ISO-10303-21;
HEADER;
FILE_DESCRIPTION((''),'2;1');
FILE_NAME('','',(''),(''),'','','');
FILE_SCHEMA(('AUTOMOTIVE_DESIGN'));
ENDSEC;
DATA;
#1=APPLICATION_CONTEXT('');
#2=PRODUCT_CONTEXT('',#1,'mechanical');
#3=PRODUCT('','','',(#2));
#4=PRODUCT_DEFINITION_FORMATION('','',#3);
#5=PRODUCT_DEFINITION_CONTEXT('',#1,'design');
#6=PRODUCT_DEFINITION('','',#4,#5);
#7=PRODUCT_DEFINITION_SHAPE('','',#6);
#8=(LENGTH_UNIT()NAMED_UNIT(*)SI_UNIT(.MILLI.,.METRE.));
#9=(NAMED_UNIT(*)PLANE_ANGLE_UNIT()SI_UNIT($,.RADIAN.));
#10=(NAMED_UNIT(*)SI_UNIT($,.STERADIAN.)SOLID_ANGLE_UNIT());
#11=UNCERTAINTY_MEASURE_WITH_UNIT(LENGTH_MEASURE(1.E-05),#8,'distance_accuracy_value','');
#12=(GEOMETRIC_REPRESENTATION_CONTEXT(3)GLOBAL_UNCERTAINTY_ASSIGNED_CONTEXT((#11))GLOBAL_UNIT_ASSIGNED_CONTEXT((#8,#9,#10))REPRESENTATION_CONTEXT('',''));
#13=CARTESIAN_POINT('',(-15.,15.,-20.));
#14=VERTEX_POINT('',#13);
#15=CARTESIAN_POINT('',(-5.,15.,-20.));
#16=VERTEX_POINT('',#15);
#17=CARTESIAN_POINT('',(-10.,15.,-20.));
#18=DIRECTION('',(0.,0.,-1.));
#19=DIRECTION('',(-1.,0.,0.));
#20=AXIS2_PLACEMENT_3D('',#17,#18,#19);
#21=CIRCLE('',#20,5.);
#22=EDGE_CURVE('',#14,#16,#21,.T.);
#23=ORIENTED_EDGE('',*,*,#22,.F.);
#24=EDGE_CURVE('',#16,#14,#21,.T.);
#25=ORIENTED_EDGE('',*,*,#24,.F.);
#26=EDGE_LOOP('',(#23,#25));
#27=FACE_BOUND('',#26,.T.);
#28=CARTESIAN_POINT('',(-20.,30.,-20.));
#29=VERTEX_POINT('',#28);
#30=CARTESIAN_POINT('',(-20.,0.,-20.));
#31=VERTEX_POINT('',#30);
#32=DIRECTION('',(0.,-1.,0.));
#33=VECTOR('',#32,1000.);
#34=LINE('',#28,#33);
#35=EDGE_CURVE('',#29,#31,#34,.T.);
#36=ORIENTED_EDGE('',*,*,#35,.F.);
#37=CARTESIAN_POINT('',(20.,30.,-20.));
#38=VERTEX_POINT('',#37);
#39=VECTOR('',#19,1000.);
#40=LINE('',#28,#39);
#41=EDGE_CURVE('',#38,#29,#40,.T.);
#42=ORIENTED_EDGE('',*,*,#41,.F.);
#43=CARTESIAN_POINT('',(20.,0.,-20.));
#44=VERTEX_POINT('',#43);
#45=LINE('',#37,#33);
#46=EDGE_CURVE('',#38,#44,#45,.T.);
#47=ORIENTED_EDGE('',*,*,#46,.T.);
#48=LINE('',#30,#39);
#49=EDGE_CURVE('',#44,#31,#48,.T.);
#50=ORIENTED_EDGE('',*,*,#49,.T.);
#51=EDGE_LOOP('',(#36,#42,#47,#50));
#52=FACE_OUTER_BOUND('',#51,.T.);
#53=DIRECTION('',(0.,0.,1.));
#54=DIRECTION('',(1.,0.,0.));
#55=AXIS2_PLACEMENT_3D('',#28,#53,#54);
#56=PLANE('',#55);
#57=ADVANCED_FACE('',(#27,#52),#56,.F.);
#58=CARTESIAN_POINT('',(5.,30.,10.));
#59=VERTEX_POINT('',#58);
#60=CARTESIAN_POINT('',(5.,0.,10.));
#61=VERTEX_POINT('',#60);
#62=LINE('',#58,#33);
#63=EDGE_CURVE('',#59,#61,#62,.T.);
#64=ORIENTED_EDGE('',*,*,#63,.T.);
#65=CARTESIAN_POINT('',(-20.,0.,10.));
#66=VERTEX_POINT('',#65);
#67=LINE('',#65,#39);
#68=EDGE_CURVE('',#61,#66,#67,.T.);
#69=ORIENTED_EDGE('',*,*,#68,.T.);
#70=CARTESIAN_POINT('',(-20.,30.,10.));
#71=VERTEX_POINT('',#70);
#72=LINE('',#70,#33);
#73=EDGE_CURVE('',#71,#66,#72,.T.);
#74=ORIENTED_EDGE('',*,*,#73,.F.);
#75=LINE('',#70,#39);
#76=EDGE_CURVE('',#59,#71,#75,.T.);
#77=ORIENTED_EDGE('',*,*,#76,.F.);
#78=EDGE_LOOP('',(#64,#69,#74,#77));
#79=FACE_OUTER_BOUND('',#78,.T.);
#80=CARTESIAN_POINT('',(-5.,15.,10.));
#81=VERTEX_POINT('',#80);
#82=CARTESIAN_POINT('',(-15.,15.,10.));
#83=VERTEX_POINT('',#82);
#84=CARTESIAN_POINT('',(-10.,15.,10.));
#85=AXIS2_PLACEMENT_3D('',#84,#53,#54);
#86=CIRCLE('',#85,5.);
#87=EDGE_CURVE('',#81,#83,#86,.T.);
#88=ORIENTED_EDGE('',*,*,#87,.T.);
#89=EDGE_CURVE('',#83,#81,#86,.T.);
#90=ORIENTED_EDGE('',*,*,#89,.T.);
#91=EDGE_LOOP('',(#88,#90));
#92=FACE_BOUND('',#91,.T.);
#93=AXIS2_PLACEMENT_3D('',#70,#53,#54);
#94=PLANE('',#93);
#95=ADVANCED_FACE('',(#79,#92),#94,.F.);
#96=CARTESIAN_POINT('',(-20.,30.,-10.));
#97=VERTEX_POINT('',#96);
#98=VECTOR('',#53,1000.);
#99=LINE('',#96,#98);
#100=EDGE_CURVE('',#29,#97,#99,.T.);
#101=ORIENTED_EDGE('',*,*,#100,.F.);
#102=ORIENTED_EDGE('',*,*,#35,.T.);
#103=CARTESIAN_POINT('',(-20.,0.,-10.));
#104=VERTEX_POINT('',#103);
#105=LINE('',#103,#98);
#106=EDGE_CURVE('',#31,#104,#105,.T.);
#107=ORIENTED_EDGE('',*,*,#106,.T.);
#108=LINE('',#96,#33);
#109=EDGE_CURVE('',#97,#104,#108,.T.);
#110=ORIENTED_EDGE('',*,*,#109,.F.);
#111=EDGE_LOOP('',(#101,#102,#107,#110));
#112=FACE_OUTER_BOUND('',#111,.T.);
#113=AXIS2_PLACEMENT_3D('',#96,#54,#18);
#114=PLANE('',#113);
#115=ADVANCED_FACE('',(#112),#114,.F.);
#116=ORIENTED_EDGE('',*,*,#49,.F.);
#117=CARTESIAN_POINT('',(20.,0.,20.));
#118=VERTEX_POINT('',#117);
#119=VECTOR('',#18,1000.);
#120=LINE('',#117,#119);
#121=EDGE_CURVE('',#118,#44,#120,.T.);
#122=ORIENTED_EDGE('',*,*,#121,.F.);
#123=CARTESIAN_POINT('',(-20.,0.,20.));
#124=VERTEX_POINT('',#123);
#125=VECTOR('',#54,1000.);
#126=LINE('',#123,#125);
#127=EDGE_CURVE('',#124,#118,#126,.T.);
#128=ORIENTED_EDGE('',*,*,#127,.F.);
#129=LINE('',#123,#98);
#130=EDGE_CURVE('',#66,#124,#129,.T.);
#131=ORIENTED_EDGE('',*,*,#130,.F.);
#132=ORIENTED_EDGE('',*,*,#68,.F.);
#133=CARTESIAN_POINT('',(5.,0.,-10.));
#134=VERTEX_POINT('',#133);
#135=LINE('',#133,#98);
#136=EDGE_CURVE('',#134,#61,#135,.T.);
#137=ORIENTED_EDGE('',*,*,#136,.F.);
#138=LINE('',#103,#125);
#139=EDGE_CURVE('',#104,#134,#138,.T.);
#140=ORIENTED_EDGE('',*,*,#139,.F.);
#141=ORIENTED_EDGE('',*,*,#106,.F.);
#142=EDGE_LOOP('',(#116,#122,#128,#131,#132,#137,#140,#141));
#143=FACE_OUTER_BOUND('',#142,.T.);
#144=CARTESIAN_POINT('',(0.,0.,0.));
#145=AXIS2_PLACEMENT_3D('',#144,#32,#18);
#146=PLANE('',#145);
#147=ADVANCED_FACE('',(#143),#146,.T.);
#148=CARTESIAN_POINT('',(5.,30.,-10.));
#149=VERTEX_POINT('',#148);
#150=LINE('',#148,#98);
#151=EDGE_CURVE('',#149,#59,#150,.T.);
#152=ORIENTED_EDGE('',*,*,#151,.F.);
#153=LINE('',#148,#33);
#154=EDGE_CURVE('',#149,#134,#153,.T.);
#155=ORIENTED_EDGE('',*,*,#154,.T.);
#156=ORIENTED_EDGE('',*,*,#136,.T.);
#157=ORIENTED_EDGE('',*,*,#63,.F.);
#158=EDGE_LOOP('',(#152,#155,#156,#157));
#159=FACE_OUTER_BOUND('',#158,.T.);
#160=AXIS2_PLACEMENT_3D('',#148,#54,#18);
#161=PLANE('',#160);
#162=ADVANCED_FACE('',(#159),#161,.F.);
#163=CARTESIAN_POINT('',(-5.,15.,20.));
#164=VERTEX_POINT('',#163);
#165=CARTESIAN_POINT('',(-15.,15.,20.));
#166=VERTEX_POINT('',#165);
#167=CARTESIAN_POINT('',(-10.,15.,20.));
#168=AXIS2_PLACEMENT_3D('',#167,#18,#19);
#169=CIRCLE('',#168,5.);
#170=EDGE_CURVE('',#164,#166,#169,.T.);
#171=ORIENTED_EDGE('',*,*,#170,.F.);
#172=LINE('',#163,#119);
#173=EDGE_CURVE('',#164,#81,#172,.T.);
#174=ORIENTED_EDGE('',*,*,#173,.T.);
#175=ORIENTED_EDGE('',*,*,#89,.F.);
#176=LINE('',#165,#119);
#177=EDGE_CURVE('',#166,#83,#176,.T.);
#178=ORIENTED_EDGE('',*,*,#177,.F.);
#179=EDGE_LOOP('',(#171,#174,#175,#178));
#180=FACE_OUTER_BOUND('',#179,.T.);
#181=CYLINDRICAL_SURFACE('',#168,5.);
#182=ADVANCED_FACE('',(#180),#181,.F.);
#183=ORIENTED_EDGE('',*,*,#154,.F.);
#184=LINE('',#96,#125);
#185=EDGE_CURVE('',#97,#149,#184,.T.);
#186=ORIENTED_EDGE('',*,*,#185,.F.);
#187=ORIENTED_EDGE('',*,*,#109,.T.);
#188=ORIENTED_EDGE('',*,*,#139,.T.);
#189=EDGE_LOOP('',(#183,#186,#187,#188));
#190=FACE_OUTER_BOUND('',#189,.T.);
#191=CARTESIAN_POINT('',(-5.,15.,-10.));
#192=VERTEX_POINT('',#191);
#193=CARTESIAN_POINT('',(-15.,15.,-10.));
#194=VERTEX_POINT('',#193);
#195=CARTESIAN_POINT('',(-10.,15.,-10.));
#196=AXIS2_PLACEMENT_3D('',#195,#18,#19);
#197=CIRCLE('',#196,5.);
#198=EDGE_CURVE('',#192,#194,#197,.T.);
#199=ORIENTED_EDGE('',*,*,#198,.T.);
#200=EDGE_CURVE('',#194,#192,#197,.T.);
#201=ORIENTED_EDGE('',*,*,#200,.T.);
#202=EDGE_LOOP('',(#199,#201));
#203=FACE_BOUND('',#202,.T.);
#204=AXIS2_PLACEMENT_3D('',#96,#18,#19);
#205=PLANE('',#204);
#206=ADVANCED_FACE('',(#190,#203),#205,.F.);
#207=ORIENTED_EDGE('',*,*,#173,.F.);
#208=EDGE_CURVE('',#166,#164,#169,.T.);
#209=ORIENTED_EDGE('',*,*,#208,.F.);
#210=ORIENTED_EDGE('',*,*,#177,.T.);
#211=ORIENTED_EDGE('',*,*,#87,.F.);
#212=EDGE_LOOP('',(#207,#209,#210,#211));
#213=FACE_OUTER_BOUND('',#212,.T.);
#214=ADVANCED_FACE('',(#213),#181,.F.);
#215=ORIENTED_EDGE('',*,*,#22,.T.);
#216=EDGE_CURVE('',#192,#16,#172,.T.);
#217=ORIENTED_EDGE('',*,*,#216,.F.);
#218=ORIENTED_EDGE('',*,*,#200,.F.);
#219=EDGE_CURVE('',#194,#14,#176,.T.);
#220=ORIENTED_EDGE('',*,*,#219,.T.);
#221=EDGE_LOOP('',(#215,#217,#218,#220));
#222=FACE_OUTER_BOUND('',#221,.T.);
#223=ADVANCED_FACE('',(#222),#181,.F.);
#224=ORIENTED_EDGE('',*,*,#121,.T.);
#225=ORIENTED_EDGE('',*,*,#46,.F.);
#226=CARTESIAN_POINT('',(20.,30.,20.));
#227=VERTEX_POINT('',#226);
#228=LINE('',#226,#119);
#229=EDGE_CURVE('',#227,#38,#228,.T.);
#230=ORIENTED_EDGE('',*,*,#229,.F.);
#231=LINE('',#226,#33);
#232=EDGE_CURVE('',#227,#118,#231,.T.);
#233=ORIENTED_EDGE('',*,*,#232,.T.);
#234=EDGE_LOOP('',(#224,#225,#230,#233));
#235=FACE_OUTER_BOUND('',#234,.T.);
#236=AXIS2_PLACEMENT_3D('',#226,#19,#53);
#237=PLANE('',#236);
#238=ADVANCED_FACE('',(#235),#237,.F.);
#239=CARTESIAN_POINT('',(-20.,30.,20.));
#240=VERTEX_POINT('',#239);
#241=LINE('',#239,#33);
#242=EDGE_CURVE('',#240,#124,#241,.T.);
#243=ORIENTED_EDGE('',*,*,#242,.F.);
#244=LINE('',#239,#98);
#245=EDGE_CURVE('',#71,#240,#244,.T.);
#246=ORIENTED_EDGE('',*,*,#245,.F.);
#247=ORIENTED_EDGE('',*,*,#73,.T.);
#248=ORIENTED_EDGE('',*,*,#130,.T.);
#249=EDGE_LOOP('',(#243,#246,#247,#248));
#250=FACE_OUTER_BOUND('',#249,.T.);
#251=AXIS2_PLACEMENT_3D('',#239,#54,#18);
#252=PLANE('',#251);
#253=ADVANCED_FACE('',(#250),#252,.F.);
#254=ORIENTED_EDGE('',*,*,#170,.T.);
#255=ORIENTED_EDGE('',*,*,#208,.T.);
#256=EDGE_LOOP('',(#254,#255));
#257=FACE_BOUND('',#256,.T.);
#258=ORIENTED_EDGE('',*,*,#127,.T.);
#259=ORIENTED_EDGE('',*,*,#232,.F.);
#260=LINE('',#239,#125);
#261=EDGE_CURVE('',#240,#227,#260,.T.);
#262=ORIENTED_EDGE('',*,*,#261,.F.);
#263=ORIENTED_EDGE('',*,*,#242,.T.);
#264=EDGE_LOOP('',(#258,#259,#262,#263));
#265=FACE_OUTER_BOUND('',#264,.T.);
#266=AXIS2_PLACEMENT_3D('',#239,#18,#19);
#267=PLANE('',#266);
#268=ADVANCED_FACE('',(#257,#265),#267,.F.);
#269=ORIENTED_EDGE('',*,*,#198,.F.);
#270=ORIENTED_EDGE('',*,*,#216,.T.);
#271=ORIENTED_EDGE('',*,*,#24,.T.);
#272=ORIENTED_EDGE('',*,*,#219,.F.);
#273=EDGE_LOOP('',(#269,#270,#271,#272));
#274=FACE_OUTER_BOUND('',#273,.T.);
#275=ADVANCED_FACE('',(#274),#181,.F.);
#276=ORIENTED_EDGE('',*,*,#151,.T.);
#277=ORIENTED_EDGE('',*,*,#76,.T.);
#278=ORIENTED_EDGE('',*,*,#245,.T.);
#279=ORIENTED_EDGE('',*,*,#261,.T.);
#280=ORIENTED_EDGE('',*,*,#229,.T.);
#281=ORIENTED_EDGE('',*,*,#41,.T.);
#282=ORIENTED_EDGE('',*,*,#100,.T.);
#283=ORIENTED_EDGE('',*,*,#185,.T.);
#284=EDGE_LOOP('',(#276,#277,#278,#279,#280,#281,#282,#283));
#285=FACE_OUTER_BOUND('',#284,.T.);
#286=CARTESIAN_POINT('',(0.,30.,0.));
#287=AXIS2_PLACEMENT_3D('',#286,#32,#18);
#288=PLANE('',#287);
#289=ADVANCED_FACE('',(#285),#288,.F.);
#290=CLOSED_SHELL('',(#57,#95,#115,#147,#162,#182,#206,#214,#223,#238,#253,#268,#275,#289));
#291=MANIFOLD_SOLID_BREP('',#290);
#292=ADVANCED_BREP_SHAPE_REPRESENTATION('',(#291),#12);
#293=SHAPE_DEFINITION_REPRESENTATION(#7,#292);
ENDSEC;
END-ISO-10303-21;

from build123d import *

# Parameters (mm, degrees)
BOSS_EXTRUDE1_DEPTH = 30
SKETCH2_R           = 5
CUT_EXTRUDE1_DEPTH  = 54.851648071


with BuildPart() as part:
    # Sketch1 → Boss-Extrude1 (new body)
    with BuildSketch(Plane(origin=(0, 0, 0), x_dir=(1, 0, 0), z_dir=(0, 1, 0))):
        Polygon((-20, 10), (-20, 20), (20, 20), (20, -20), (-20, -20), (-20, -10), (5, -10), (5, 10), align=None)
    extrude(amount=BOSS_EXTRUDE1_DEPTH)

    # Sketch2 → Cut-Extrude1 (cut, through all)
    with BuildSketch(Plane(origin=(0, 0, -20), x_dir=(-1, 0, 0), z_dir=(0, 0, -1))):
        with Locations((10, 15)):
            Circle(SKETCH2_R)
    extrude(amount=-CUT_EXTRUDE1_DEPTH, mode=Mode.SUBTRACT)


solid = part.part
